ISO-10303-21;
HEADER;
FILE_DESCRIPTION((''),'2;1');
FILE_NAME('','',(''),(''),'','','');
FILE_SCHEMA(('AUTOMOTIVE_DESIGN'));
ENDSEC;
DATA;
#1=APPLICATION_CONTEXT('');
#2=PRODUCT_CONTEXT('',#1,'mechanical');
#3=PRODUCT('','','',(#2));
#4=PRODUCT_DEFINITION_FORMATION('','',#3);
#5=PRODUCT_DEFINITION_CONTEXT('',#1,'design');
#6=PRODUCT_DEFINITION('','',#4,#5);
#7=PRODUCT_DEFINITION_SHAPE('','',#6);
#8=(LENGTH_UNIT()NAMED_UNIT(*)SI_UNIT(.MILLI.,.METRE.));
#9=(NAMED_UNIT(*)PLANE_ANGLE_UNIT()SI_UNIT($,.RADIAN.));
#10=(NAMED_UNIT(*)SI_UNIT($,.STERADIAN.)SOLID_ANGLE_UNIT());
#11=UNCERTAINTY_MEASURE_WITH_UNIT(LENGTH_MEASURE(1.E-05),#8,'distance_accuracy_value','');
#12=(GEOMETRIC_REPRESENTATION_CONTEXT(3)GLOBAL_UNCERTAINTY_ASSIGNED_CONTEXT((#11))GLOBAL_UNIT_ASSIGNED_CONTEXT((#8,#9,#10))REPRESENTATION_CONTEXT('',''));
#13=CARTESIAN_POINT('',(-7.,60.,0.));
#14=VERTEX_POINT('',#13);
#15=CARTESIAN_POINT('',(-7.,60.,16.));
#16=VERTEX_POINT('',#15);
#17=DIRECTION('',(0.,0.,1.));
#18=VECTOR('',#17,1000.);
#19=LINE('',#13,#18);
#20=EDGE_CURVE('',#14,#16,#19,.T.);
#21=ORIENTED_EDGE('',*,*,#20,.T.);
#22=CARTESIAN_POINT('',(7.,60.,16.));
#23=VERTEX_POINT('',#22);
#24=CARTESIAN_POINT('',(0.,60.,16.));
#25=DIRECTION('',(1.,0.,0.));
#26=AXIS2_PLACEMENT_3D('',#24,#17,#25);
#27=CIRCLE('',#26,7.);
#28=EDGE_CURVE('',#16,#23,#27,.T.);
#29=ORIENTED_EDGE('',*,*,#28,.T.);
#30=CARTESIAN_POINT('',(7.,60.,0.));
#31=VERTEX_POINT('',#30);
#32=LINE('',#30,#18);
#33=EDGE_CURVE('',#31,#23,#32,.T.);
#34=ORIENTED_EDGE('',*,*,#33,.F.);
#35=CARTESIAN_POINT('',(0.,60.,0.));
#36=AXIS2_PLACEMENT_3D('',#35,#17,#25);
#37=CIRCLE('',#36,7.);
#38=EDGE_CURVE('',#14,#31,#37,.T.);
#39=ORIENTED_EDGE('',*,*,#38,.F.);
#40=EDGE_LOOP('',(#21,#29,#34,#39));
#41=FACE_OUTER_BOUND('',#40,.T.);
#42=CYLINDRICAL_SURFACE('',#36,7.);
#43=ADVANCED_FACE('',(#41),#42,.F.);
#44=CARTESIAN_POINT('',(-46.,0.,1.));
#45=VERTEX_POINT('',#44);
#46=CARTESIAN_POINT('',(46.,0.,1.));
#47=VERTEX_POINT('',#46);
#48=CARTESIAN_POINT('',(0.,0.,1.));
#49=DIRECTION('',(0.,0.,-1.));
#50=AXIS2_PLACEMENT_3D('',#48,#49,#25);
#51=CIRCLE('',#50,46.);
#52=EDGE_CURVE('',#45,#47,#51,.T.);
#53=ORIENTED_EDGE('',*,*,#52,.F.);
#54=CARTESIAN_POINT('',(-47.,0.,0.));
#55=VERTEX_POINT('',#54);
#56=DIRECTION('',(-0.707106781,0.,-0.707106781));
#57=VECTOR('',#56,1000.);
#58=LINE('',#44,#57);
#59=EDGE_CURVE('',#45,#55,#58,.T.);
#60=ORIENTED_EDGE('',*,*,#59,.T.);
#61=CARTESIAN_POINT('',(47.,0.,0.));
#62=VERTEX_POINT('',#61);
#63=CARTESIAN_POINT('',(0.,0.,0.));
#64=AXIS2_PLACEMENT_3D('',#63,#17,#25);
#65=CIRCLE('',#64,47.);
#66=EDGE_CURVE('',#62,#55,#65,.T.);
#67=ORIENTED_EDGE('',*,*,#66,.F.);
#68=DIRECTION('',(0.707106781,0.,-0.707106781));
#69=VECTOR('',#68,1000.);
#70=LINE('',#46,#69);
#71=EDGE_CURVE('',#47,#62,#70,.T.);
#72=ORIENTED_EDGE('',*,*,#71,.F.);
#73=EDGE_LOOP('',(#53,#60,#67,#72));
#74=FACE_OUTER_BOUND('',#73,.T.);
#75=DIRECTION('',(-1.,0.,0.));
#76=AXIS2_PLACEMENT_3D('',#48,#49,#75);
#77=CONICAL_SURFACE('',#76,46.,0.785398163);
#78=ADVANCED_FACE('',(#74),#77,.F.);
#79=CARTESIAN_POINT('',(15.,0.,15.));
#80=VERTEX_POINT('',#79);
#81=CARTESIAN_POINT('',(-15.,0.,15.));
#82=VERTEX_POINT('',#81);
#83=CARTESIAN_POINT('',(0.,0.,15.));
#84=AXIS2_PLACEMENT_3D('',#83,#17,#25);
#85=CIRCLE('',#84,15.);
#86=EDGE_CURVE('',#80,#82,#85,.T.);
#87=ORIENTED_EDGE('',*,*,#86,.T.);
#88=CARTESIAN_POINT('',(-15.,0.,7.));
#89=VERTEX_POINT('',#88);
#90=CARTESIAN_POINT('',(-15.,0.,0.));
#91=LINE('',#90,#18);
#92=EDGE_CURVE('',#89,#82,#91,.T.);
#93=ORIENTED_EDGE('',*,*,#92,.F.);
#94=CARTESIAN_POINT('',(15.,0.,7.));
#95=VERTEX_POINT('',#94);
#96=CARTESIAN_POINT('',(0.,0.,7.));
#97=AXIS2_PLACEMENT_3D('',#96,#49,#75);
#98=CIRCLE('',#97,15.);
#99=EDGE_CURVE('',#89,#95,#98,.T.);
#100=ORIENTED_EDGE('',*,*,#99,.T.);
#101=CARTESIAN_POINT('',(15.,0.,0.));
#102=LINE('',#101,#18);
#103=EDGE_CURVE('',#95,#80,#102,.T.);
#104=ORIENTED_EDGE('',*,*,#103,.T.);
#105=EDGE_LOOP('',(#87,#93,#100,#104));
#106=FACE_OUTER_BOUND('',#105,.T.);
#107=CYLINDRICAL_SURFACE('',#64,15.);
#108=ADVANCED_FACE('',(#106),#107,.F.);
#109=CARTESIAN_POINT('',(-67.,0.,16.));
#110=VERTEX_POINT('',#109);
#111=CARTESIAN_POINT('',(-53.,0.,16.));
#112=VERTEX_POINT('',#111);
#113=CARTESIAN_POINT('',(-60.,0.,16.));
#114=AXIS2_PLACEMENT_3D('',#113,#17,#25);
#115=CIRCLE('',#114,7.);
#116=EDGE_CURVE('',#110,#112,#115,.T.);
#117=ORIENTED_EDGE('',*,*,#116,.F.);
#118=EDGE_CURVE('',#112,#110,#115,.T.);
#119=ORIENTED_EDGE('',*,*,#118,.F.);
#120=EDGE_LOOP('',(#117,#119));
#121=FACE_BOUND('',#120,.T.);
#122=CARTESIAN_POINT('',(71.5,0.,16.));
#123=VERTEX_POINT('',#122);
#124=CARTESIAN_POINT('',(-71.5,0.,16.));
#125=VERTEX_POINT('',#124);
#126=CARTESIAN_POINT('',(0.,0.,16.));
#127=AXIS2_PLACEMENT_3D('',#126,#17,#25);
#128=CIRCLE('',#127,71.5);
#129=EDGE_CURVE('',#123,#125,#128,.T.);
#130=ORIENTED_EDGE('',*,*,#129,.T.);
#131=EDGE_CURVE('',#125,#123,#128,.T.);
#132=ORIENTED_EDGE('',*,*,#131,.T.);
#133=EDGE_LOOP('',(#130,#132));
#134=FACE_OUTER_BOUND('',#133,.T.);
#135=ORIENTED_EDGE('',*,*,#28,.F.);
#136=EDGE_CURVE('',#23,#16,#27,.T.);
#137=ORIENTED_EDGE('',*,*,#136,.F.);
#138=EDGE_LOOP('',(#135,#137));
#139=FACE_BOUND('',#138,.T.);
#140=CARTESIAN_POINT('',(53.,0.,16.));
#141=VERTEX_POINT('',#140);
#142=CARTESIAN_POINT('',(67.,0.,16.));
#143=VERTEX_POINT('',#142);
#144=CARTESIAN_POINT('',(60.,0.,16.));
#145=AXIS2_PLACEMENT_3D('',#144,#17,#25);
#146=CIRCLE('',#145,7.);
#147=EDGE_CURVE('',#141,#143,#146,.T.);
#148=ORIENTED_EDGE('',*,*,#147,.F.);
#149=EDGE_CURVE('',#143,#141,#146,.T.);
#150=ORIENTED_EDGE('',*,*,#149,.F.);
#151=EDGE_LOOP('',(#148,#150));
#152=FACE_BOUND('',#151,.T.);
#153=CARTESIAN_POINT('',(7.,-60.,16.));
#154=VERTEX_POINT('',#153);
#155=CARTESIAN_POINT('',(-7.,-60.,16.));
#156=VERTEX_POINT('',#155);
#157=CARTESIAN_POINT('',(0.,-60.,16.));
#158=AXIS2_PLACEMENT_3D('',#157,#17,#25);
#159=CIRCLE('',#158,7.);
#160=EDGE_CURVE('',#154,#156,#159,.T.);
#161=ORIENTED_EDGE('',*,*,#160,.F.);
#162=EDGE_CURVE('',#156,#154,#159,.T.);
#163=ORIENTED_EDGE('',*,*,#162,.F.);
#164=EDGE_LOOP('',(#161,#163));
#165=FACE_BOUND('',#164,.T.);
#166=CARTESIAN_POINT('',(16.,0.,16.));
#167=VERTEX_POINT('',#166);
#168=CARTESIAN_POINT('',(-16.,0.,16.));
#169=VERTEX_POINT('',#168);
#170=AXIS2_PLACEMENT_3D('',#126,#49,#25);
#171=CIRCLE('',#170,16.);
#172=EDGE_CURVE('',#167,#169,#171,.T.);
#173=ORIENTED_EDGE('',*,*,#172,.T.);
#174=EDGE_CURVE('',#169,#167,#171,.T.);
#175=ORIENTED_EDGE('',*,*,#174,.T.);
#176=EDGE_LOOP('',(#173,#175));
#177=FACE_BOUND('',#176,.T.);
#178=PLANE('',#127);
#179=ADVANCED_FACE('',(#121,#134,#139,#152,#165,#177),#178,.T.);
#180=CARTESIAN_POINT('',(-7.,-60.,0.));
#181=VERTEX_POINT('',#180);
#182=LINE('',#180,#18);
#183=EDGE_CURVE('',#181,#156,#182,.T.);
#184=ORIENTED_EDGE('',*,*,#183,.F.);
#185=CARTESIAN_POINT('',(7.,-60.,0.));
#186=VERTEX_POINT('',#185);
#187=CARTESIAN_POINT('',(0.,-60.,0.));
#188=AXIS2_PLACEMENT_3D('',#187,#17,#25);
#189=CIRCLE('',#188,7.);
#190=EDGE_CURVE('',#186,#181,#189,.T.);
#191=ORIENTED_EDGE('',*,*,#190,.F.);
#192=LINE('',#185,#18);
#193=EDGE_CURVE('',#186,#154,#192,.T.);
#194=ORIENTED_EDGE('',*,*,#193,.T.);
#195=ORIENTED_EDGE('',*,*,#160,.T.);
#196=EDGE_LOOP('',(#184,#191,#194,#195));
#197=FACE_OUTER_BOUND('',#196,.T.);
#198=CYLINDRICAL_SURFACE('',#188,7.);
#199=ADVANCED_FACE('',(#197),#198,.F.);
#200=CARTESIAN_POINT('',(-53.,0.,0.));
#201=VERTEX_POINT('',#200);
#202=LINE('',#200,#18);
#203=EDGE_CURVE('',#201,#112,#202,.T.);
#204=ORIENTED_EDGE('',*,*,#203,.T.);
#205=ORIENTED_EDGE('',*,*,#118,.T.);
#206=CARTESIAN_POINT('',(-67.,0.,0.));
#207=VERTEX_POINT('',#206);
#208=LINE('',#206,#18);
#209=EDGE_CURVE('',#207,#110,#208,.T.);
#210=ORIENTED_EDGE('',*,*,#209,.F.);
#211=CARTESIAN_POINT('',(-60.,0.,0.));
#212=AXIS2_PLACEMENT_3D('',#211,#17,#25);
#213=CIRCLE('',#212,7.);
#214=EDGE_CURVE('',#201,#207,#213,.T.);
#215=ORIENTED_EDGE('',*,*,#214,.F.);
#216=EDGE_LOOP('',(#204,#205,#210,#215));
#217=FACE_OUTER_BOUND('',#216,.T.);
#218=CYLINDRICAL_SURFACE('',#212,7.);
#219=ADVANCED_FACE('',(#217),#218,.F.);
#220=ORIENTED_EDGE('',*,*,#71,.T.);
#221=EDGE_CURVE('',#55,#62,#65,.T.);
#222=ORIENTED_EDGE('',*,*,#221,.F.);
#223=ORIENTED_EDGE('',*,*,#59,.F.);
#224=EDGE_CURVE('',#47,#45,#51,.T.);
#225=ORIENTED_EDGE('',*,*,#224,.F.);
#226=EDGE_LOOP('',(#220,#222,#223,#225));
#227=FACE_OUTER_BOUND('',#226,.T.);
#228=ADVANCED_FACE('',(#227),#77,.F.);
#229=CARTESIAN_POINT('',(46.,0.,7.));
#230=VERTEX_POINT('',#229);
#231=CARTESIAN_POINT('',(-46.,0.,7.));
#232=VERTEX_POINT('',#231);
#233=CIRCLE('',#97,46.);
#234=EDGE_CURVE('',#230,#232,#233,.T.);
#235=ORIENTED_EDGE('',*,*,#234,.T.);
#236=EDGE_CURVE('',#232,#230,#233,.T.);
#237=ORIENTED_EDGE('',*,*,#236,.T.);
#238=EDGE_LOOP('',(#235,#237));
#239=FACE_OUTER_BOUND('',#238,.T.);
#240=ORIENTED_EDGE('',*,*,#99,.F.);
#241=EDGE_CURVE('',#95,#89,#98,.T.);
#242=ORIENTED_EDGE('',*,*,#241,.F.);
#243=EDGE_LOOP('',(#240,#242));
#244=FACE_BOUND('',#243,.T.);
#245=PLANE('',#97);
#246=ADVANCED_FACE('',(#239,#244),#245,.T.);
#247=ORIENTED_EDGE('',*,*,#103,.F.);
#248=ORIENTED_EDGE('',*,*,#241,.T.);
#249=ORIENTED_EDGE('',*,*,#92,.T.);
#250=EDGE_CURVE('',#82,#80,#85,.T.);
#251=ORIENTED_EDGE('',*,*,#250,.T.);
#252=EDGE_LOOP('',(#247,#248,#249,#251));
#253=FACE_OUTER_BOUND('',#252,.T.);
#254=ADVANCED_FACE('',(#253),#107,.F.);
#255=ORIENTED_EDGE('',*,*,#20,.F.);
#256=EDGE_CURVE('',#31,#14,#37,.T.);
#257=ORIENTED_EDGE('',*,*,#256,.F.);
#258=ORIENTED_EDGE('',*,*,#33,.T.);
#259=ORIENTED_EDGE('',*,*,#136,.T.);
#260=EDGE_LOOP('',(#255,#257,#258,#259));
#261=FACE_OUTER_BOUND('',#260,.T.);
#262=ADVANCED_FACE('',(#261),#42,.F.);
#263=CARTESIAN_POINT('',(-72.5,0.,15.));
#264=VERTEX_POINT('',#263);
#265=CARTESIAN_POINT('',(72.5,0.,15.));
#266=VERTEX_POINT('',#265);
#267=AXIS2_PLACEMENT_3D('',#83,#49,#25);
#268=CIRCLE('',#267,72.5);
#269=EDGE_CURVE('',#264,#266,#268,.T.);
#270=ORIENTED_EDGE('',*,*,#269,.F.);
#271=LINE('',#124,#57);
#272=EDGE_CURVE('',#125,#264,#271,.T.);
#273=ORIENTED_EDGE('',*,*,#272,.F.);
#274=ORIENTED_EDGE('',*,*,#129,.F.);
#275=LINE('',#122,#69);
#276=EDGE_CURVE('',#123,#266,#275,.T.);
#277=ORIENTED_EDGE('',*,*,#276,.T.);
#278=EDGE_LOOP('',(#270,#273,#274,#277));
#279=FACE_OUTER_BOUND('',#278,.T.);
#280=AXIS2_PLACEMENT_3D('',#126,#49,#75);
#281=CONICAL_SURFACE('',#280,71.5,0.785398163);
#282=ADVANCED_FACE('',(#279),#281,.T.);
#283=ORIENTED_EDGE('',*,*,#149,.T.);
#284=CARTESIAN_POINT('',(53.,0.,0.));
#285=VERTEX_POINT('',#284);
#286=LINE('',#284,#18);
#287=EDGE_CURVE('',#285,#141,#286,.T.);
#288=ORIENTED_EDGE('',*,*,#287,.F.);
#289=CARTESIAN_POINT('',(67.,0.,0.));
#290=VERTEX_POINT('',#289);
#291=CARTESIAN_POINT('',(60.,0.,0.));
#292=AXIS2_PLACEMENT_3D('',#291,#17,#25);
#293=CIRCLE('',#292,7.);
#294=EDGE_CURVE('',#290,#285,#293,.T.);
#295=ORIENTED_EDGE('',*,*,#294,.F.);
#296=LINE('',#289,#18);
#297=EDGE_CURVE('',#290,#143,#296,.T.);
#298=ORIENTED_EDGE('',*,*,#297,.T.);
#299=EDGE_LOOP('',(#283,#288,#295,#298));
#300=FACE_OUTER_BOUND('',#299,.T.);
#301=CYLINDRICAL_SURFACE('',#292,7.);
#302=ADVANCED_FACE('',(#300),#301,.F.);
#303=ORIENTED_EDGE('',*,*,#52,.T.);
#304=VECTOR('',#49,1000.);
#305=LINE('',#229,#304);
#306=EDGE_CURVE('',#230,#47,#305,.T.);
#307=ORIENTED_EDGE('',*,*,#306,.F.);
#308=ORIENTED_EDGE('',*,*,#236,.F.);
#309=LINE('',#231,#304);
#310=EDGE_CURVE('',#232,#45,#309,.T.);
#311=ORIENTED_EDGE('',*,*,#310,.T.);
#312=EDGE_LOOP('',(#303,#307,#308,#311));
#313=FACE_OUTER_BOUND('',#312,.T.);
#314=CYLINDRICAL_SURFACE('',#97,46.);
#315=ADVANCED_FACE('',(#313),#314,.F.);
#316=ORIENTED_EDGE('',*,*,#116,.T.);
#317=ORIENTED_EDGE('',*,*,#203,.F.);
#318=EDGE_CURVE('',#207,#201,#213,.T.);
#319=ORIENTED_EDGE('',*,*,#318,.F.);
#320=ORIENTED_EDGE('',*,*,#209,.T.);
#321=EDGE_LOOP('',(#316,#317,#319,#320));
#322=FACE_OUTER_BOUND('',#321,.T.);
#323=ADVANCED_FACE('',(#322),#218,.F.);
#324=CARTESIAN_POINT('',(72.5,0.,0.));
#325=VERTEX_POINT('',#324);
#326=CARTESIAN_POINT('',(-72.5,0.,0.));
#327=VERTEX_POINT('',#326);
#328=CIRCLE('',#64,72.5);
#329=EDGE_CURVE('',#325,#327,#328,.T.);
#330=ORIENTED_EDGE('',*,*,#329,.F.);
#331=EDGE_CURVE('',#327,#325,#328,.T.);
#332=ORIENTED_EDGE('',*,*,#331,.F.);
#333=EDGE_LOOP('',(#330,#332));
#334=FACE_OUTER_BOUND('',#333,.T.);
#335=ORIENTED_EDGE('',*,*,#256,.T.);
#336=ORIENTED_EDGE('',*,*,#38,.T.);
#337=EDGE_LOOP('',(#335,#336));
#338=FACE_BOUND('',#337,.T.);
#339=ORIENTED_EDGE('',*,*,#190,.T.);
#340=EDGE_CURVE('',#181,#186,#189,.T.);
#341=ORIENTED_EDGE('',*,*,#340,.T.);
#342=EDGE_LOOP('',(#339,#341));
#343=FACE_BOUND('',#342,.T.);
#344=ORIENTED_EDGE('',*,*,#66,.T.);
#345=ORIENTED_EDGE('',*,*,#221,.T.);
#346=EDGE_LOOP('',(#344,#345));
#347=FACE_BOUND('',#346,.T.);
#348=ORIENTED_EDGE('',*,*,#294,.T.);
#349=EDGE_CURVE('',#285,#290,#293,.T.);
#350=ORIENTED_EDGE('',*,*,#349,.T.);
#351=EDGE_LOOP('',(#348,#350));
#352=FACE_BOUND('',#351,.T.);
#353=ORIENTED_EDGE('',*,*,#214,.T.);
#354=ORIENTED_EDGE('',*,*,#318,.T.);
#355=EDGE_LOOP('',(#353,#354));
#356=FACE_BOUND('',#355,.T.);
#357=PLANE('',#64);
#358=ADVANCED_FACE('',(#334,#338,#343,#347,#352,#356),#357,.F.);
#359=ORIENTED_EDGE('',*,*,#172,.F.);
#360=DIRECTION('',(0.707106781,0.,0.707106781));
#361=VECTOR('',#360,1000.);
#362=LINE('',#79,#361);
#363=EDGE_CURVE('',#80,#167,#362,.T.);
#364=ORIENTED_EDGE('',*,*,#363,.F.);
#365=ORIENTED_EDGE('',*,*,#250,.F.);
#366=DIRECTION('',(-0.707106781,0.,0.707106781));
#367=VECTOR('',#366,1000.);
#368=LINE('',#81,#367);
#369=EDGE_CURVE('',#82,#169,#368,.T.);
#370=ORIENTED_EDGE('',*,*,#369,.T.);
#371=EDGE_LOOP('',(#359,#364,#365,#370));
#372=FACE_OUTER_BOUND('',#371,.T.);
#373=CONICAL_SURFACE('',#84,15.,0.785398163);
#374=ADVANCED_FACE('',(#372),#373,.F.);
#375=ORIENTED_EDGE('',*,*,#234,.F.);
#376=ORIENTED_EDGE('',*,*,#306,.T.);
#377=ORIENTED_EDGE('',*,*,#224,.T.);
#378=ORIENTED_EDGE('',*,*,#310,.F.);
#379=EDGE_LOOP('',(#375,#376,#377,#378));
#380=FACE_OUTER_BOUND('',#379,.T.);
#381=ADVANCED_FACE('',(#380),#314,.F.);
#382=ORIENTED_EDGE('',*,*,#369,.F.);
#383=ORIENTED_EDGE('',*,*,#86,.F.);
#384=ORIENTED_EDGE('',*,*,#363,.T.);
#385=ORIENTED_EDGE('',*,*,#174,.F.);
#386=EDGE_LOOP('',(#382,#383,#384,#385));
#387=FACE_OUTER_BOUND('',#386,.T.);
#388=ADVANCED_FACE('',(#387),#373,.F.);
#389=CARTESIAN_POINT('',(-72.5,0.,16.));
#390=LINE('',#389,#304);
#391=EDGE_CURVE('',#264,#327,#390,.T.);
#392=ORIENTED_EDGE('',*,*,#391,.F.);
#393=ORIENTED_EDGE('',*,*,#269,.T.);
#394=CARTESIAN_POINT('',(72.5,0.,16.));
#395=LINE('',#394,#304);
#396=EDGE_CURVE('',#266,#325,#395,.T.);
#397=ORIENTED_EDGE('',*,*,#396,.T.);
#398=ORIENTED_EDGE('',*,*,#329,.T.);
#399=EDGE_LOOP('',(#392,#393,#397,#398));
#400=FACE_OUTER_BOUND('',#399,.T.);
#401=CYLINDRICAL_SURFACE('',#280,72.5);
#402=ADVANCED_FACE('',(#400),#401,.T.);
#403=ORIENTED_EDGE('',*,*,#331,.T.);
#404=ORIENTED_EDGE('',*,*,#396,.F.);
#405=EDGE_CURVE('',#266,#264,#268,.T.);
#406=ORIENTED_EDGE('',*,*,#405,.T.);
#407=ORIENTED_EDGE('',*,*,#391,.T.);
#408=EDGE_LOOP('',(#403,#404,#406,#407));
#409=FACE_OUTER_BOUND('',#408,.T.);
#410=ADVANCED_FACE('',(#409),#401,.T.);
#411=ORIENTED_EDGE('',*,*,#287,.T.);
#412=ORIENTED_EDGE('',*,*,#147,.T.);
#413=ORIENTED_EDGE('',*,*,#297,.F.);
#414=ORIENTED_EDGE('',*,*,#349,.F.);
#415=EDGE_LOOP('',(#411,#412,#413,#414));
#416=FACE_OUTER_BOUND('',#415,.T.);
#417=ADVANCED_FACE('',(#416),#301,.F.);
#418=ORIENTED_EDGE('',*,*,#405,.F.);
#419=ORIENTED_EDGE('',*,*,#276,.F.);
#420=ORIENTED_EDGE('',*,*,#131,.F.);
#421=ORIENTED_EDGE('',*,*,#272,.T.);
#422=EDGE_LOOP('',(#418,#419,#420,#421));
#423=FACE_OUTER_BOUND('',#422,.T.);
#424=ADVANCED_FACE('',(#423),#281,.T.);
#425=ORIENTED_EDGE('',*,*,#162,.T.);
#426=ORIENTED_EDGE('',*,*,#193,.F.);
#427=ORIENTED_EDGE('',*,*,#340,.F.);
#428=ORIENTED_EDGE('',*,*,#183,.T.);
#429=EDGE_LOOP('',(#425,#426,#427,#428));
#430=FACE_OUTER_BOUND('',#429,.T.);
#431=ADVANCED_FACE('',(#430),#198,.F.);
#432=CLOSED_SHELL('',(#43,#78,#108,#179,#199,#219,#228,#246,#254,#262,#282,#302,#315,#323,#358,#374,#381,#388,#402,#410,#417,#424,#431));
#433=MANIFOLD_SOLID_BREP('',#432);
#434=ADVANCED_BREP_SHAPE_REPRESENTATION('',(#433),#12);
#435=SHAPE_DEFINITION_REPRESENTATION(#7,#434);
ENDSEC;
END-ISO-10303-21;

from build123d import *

# Parameters (mm, degrees)
SKETCH_1_R          = 72.5
EXTRUDE_1_DEPTH     = 16
SKETCH_2_R          = 7
CUT_EXTRUDE_1_DEPTH = 104.771383339
SKETCH_3_R          = 46
CUT_EXTRUDE_2_DEPTH = 7
SKETCH_4_R          = 15
CUT_EXTRUDE_3_DEPTH = 104.771383339
CHAMFER_1_SIZE      = 1


with BuildPart() as part:
    # 草图1 → 凸台-拉伸1 (new body)
    with BuildSketch(Plane.XY):
        Circle(SKETCH_1_R)
    extrude(amount=EXTRUDE_1_DEPTH)

    # 草图2 → 切除-拉伸1 (cut, through all)
    with BuildSketch(Plane.XY.offset(16)):
        with Locations((0, 60)):
            Circle(SKETCH_2_R)
        with Locations((60, 0)):
            Circle(SKETCH_2_R)
        with Locations((0, -60)):
            Circle(SKETCH_2_R)
        with Locations((-60, 0)):
            Circle(SKETCH_2_R)
    extrude(amount=-CUT_EXTRUDE_1_DEPTH, mode=Mode.SUBTRACT)

    # 草图3 → 切除-拉伸2 (cut)
    with BuildSketch(Plane(origin=(0, 0, 0), x_dir=(-1, 0, 0), z_dir=(0, 0, -1))):
        Circle(SKETCH_3_R)
    extrude(amount=-CUT_EXTRUDE_2_DEPTH, mode=Mode.SUBTRACT)

    # 草图4 → 切除-拉伸3 (cut, through all)
    with BuildSketch(Plane.XY.offset(16)):
        Circle(SKETCH_4_R)
    extrude(amount=-CUT_EXTRUDE_3_DEPTH, mode=Mode.SUBTRACT)

    # 倒角1
    chamfer_1_edges = [part.edges().sort_by_distance(p)[0] for p in [
        (46, 0, 0),
        (-15, 0, 16),
        (-72.5, 0, 16),
    ]]
    chamfer(chamfer_1_edges, length=CHAMFER_1_SIZE)


solid = part.part
